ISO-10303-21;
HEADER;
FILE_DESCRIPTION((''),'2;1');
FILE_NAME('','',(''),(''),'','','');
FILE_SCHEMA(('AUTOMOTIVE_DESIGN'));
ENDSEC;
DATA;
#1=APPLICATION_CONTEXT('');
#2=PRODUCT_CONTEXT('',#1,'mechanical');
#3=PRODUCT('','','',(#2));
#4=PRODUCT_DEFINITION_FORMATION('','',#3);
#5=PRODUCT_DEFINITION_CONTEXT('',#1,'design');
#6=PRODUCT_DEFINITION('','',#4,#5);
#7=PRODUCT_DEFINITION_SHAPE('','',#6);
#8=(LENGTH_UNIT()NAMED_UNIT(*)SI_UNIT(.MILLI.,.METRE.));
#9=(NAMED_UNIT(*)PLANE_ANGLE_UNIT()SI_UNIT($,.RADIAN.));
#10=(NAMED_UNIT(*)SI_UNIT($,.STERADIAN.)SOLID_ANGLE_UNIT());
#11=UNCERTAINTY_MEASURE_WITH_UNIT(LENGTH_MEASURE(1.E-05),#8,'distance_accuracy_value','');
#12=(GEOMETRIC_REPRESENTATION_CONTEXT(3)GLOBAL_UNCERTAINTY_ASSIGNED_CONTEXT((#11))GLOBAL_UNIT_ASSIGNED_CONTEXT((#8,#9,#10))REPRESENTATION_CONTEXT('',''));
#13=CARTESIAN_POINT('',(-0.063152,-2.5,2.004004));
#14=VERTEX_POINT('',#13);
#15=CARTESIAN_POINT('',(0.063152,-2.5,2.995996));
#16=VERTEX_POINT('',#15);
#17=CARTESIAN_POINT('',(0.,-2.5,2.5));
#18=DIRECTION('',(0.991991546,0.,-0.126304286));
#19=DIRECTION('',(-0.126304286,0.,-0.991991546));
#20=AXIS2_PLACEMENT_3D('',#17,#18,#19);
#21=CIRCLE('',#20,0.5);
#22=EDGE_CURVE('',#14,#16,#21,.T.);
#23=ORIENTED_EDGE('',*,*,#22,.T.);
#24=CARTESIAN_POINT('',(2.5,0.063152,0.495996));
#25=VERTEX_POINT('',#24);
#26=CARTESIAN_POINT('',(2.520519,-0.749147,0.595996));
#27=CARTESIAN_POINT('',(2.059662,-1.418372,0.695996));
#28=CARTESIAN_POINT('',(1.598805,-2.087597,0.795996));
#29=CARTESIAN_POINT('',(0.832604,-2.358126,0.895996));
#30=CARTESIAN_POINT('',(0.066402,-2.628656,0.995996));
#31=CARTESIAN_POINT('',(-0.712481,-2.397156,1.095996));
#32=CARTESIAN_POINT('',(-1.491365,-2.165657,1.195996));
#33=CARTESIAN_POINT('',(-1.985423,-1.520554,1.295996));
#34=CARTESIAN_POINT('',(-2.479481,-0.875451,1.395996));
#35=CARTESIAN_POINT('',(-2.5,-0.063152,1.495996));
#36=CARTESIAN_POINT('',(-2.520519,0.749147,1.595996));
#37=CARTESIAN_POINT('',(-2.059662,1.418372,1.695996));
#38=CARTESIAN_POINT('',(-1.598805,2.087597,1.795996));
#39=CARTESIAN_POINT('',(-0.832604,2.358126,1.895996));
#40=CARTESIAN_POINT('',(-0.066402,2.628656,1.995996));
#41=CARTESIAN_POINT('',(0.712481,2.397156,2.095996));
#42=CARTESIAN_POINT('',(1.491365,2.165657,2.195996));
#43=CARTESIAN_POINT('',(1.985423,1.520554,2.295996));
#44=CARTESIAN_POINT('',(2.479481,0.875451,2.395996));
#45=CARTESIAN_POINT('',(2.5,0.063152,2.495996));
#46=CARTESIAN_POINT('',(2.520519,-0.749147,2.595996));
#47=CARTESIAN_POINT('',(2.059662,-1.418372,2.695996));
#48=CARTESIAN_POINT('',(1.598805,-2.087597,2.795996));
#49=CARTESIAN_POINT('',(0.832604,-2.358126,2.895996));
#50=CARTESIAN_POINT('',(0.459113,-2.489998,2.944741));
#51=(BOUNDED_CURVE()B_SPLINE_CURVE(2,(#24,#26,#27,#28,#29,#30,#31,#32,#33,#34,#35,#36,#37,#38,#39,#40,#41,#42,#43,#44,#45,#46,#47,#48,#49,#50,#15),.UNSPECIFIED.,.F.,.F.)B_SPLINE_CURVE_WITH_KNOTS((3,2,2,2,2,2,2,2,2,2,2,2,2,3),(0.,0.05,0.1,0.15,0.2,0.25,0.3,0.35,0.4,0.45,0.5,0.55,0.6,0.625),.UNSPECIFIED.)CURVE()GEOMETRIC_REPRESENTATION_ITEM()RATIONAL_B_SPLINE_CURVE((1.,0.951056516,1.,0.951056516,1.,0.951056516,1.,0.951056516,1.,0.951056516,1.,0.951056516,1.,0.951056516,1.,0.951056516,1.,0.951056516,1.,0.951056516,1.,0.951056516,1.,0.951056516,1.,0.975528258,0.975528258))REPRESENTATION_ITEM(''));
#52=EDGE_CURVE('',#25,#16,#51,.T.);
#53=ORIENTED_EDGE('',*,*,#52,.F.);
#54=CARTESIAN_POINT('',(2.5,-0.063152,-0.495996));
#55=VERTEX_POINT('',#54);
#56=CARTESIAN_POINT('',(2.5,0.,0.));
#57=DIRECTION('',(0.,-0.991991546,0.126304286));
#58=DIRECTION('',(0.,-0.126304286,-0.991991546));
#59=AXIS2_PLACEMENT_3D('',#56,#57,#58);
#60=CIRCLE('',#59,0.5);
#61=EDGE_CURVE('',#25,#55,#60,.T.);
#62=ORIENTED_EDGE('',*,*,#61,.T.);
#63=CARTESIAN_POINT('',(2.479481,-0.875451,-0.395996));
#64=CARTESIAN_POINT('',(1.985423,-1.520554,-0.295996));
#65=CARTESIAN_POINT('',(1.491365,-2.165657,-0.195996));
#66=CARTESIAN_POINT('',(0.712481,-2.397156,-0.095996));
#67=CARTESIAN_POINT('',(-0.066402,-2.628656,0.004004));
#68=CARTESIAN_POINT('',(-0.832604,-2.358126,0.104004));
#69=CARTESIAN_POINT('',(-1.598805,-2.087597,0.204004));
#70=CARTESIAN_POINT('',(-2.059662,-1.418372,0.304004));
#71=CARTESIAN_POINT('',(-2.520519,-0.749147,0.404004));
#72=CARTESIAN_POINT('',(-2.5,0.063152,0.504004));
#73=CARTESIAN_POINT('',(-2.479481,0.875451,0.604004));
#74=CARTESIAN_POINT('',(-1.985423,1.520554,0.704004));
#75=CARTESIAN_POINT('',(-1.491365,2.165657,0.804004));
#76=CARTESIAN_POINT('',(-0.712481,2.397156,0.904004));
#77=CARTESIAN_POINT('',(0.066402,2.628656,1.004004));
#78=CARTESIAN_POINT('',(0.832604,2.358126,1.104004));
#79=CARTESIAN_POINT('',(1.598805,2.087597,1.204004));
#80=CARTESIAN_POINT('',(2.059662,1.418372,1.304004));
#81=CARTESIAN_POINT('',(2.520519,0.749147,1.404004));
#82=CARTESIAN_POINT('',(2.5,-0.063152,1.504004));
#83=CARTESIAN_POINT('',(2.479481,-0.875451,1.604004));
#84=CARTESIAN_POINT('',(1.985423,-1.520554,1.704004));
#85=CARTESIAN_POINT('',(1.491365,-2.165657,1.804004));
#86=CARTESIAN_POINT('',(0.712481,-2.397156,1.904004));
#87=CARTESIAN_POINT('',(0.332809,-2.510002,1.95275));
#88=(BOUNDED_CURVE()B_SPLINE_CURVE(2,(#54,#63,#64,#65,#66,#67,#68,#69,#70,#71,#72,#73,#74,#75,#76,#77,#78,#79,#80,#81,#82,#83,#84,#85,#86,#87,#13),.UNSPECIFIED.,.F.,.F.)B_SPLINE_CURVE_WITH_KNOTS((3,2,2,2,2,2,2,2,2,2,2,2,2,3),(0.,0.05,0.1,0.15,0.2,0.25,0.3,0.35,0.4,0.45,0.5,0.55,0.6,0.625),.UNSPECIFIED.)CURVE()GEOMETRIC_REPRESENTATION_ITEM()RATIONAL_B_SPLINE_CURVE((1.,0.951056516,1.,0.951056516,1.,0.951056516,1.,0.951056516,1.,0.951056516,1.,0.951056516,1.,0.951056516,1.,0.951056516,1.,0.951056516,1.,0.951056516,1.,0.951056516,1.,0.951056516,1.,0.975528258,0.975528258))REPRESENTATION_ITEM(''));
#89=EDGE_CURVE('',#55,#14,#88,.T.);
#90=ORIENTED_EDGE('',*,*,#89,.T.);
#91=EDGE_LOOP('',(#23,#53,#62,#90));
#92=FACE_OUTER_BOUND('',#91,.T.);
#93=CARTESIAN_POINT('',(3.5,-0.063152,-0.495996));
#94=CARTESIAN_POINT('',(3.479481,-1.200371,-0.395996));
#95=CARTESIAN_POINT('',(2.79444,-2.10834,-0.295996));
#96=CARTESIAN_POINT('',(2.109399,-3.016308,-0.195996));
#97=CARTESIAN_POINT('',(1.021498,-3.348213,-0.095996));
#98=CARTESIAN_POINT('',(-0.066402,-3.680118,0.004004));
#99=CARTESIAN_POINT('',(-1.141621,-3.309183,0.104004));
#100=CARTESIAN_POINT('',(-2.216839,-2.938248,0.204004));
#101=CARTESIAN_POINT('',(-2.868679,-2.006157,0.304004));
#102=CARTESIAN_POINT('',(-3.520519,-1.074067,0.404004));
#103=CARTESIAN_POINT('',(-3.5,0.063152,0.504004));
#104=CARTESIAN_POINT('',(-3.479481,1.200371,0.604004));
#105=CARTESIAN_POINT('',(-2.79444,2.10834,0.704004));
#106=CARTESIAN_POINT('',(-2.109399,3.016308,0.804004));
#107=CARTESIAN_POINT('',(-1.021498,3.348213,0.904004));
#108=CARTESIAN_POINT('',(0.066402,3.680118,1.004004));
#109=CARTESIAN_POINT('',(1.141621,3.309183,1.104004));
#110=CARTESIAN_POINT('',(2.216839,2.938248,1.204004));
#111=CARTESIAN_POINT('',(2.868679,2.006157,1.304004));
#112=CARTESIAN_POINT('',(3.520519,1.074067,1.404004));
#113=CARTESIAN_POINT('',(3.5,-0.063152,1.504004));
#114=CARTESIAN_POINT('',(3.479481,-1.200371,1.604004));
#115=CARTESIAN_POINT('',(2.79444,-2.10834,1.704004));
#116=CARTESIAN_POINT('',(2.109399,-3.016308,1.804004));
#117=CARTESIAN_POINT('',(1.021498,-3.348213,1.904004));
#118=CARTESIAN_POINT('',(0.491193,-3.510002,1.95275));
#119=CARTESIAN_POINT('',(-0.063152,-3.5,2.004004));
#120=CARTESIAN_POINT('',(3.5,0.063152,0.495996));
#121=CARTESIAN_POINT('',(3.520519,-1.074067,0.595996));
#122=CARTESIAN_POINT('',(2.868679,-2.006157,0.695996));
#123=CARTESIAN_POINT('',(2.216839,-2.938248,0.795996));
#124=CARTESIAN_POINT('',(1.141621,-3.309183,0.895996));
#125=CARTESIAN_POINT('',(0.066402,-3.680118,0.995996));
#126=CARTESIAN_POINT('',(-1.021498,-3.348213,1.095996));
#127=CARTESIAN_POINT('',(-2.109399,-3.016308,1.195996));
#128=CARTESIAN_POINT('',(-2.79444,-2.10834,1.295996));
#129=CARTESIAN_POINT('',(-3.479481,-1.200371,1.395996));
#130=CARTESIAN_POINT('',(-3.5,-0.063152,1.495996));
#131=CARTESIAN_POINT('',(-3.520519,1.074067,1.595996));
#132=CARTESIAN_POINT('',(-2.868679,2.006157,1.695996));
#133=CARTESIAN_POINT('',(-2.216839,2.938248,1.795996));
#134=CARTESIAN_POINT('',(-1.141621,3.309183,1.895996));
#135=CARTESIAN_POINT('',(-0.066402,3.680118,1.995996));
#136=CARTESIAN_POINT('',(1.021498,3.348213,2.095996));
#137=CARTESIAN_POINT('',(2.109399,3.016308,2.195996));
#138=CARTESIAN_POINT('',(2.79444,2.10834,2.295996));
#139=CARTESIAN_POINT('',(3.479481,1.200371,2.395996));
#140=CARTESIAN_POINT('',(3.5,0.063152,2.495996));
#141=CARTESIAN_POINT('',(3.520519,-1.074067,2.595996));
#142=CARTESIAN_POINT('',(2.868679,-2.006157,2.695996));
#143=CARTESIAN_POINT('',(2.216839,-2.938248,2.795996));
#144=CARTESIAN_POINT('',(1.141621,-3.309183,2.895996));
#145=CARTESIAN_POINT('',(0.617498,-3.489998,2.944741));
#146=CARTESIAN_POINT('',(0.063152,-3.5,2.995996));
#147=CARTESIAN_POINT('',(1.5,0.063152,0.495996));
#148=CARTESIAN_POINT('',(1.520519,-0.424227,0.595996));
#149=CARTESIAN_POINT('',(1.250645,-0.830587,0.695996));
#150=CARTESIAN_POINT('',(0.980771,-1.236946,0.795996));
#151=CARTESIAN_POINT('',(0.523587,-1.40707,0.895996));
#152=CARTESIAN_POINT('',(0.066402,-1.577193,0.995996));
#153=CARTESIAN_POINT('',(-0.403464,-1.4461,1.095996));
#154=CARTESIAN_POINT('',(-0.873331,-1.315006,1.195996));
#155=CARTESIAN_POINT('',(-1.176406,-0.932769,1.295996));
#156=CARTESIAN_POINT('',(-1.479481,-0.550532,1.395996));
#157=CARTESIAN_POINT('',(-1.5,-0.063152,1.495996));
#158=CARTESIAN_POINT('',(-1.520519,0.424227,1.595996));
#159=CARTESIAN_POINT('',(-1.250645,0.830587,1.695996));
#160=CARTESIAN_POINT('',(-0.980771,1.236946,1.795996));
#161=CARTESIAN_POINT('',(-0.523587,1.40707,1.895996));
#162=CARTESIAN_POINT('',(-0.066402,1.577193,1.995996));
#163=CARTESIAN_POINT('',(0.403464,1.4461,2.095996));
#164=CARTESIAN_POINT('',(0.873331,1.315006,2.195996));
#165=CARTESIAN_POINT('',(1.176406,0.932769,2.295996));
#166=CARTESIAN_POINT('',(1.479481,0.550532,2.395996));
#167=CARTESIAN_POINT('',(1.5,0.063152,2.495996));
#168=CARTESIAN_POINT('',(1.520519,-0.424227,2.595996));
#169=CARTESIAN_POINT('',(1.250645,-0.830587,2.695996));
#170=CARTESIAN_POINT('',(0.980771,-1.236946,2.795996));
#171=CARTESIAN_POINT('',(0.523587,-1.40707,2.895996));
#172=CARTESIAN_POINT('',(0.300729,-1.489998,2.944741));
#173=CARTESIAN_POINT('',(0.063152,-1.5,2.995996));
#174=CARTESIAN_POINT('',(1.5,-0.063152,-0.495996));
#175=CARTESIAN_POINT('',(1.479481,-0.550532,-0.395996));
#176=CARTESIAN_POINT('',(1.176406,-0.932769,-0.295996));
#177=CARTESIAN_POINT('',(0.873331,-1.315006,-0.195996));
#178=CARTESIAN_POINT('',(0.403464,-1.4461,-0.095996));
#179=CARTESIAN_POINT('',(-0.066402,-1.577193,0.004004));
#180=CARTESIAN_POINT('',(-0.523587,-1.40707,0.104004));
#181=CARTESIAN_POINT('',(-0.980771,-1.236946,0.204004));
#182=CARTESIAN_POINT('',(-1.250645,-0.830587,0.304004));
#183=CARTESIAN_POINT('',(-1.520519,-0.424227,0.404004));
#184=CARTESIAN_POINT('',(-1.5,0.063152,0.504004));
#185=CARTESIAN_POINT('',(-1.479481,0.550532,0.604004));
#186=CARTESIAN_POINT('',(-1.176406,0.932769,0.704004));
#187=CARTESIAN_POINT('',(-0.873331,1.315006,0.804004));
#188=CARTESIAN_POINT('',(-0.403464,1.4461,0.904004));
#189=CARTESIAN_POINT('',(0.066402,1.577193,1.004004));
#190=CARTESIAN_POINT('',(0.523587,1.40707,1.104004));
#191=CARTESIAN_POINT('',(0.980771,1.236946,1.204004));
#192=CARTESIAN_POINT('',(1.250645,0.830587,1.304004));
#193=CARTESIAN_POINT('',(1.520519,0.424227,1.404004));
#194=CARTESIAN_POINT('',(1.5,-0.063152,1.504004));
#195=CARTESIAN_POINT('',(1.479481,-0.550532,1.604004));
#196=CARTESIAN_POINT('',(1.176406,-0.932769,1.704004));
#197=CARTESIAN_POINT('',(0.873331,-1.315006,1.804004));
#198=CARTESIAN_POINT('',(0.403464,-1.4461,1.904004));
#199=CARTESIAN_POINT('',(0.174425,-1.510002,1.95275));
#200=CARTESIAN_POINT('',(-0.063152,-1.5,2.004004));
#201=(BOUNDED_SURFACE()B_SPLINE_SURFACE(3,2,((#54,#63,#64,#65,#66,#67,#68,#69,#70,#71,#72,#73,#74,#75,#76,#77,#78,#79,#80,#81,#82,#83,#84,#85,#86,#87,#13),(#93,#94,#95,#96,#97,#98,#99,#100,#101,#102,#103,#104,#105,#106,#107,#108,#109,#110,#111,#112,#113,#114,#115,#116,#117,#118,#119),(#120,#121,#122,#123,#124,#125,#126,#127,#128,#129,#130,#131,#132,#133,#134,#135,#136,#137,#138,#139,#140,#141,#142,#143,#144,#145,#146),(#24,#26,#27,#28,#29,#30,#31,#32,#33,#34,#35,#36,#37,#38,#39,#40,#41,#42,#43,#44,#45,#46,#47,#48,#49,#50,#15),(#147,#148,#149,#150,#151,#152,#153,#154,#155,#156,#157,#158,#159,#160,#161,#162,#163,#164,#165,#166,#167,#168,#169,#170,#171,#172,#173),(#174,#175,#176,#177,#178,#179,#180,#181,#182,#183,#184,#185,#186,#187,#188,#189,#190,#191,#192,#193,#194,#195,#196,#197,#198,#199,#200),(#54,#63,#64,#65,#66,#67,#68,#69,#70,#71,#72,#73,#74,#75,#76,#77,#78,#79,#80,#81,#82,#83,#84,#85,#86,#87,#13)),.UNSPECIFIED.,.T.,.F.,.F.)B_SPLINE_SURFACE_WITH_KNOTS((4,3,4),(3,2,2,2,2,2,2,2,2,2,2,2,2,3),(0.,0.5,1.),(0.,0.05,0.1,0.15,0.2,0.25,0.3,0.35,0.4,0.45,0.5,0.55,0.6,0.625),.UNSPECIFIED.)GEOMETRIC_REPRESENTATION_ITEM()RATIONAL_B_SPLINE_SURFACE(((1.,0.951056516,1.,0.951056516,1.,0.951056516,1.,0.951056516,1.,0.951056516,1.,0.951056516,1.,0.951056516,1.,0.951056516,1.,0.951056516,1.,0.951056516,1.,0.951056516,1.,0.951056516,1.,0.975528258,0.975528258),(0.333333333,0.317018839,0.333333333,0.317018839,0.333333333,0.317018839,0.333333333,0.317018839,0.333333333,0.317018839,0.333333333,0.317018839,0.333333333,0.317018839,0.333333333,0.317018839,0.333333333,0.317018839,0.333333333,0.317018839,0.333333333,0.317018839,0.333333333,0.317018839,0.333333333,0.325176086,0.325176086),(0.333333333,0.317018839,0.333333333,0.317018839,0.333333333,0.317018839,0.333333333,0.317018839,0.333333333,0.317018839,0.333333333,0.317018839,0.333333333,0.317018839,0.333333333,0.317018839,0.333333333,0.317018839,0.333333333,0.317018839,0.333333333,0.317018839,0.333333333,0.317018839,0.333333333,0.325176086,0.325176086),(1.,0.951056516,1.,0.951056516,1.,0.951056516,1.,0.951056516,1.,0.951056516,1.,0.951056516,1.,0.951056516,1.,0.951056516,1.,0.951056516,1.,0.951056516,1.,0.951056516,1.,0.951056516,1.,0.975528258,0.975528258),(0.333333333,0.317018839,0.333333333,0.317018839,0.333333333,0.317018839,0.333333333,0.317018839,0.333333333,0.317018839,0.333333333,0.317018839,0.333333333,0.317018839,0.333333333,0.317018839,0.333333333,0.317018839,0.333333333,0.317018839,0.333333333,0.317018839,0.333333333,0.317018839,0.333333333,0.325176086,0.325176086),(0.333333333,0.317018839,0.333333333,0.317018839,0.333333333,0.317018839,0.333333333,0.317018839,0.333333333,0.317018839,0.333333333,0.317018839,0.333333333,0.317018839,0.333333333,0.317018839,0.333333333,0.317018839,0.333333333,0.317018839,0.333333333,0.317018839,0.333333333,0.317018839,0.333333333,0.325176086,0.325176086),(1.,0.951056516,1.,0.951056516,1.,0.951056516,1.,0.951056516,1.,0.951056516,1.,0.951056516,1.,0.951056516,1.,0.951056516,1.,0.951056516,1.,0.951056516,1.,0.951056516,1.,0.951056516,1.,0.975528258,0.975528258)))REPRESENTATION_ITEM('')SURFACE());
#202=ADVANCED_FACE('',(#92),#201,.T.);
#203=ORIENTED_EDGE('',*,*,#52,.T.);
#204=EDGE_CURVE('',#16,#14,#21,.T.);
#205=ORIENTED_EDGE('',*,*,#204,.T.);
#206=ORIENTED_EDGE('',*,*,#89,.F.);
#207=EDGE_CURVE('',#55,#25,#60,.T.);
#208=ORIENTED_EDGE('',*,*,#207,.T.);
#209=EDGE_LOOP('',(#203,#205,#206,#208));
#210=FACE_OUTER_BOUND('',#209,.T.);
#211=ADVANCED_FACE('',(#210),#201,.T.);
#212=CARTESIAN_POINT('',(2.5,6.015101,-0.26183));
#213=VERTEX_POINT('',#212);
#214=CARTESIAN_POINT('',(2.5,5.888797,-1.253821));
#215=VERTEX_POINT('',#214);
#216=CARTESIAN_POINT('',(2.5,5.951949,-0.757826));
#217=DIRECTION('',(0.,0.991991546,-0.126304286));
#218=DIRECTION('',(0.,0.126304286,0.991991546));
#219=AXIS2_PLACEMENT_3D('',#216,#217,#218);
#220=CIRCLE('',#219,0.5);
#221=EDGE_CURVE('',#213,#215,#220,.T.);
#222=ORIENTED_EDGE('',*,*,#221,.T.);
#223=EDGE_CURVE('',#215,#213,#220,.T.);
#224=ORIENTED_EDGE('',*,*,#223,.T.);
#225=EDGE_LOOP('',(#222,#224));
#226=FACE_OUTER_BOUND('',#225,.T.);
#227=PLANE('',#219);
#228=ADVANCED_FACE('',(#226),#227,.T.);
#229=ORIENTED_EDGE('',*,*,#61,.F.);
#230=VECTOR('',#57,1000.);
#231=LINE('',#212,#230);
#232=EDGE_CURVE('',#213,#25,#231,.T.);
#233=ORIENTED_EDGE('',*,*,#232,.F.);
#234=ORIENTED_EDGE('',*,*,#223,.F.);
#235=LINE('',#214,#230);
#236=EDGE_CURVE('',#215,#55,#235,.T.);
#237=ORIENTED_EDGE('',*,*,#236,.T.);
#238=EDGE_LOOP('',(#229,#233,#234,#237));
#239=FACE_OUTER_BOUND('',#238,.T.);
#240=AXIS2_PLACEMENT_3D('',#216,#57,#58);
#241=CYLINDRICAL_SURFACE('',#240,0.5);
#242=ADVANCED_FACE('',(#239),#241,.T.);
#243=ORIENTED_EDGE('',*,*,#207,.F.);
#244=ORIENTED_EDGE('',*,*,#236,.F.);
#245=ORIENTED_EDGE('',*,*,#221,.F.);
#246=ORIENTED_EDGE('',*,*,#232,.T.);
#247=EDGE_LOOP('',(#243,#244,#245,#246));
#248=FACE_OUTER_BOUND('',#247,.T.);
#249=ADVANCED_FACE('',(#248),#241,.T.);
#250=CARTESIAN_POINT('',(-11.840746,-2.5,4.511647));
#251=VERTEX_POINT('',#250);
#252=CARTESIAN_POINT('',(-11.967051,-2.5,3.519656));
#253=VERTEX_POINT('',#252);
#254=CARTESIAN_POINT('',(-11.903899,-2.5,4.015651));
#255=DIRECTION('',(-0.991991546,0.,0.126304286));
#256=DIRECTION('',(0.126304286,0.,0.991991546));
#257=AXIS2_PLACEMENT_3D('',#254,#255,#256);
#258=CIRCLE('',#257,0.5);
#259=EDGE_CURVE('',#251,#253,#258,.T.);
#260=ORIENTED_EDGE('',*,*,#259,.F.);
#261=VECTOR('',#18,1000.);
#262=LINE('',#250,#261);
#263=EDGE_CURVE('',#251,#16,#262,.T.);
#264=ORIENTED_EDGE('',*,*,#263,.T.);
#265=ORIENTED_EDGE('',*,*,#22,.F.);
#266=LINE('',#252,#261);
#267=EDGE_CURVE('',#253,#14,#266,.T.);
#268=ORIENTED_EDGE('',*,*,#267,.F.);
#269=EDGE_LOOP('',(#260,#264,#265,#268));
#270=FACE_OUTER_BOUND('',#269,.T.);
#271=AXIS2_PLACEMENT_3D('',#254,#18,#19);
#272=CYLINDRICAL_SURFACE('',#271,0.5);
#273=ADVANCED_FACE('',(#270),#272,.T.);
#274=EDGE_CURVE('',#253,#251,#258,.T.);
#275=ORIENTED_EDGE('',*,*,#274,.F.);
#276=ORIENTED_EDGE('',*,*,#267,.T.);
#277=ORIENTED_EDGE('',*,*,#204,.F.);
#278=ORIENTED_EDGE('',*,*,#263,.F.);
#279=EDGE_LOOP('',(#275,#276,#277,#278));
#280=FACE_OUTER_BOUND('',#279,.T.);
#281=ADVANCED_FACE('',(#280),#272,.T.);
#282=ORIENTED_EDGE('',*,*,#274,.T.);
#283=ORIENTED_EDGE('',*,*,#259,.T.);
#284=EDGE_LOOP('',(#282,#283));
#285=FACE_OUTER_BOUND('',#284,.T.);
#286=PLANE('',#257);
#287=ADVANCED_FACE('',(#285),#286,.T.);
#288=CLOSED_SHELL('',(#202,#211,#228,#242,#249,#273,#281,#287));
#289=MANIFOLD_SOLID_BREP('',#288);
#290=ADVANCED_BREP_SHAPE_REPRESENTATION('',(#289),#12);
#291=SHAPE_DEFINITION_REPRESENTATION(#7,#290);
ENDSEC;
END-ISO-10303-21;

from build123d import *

# Parameters (mm, degrees)
SWEEP1_PITCH        = 2
SWEEP1_HEIGHT       = 2.5
SWEEP1_RADIUS       = 2.5
SWEEP1_PROFILE_R    = 0.5
SKETCH8_R           = 0.5
BOSS_EXTRUDE1_DEPTH = 12
SKETCH9_R           = 0.5
BOSS_EXTRUDE2_DEPTH = 6


with BuildPart() as part:
    # Sweep1: sweep along a helix
    with BuildLine() as sweep1_path:
        Helix(SWEEP1_PITCH, SWEEP1_HEIGHT, SWEEP1_RADIUS, center=(0, 0, 0), direction=(0, 0, 1), lefthand=True)
    # Sweep1 profile (on start of the path) → Sweep1 (sweep)
    with BuildSketch(Plane(origin=(2.5, 0, 0), x_dir=(0, -0.1263042864341026, -0.9919915459460187), z_dir=(1.6922325878761384e-13, -0.9919915459460187, 0.1263042864341026))):
        Circle(SWEEP1_PROFILE_R)
    sweep(path=sweep1_path.line, is_frenet=True)

    # Sketch8 → Boss-Extrude1 (add)
    with BuildSketch(Plane(origin=(-0.313231961, 0, 0.039881932), x_dir=(0.03140455580062002, 0.9685954441994059, 0.2466508044809937), z_dir=(-0.9919915459460137, 2.652392194768538e-14, 0.12630428643414296))):
        with Locations(Location((-1.804861599, -3.023701337, 0), (0, 0, 104.397169825))):
            Circle(SKETCH8_R)
    extrude(amount=BOSS_EXTRUDE1_DEPTH)

    # Sketch9 → Boss-Extrude2 (add)
    with BuildSketch(Plane(origin=(0, 0, 0), x_dir=(1, 0, 0), z_dir=(0, 0.9919915459460136, -0.12630428643414301))):
        with Locations(Location((2.5, 0, 0), (0, 0, 90))):
            Circle(SKETCH9_R)
    extrude(amount=BOSS_EXTRUDE2_DEPTH)


solid = part.part
